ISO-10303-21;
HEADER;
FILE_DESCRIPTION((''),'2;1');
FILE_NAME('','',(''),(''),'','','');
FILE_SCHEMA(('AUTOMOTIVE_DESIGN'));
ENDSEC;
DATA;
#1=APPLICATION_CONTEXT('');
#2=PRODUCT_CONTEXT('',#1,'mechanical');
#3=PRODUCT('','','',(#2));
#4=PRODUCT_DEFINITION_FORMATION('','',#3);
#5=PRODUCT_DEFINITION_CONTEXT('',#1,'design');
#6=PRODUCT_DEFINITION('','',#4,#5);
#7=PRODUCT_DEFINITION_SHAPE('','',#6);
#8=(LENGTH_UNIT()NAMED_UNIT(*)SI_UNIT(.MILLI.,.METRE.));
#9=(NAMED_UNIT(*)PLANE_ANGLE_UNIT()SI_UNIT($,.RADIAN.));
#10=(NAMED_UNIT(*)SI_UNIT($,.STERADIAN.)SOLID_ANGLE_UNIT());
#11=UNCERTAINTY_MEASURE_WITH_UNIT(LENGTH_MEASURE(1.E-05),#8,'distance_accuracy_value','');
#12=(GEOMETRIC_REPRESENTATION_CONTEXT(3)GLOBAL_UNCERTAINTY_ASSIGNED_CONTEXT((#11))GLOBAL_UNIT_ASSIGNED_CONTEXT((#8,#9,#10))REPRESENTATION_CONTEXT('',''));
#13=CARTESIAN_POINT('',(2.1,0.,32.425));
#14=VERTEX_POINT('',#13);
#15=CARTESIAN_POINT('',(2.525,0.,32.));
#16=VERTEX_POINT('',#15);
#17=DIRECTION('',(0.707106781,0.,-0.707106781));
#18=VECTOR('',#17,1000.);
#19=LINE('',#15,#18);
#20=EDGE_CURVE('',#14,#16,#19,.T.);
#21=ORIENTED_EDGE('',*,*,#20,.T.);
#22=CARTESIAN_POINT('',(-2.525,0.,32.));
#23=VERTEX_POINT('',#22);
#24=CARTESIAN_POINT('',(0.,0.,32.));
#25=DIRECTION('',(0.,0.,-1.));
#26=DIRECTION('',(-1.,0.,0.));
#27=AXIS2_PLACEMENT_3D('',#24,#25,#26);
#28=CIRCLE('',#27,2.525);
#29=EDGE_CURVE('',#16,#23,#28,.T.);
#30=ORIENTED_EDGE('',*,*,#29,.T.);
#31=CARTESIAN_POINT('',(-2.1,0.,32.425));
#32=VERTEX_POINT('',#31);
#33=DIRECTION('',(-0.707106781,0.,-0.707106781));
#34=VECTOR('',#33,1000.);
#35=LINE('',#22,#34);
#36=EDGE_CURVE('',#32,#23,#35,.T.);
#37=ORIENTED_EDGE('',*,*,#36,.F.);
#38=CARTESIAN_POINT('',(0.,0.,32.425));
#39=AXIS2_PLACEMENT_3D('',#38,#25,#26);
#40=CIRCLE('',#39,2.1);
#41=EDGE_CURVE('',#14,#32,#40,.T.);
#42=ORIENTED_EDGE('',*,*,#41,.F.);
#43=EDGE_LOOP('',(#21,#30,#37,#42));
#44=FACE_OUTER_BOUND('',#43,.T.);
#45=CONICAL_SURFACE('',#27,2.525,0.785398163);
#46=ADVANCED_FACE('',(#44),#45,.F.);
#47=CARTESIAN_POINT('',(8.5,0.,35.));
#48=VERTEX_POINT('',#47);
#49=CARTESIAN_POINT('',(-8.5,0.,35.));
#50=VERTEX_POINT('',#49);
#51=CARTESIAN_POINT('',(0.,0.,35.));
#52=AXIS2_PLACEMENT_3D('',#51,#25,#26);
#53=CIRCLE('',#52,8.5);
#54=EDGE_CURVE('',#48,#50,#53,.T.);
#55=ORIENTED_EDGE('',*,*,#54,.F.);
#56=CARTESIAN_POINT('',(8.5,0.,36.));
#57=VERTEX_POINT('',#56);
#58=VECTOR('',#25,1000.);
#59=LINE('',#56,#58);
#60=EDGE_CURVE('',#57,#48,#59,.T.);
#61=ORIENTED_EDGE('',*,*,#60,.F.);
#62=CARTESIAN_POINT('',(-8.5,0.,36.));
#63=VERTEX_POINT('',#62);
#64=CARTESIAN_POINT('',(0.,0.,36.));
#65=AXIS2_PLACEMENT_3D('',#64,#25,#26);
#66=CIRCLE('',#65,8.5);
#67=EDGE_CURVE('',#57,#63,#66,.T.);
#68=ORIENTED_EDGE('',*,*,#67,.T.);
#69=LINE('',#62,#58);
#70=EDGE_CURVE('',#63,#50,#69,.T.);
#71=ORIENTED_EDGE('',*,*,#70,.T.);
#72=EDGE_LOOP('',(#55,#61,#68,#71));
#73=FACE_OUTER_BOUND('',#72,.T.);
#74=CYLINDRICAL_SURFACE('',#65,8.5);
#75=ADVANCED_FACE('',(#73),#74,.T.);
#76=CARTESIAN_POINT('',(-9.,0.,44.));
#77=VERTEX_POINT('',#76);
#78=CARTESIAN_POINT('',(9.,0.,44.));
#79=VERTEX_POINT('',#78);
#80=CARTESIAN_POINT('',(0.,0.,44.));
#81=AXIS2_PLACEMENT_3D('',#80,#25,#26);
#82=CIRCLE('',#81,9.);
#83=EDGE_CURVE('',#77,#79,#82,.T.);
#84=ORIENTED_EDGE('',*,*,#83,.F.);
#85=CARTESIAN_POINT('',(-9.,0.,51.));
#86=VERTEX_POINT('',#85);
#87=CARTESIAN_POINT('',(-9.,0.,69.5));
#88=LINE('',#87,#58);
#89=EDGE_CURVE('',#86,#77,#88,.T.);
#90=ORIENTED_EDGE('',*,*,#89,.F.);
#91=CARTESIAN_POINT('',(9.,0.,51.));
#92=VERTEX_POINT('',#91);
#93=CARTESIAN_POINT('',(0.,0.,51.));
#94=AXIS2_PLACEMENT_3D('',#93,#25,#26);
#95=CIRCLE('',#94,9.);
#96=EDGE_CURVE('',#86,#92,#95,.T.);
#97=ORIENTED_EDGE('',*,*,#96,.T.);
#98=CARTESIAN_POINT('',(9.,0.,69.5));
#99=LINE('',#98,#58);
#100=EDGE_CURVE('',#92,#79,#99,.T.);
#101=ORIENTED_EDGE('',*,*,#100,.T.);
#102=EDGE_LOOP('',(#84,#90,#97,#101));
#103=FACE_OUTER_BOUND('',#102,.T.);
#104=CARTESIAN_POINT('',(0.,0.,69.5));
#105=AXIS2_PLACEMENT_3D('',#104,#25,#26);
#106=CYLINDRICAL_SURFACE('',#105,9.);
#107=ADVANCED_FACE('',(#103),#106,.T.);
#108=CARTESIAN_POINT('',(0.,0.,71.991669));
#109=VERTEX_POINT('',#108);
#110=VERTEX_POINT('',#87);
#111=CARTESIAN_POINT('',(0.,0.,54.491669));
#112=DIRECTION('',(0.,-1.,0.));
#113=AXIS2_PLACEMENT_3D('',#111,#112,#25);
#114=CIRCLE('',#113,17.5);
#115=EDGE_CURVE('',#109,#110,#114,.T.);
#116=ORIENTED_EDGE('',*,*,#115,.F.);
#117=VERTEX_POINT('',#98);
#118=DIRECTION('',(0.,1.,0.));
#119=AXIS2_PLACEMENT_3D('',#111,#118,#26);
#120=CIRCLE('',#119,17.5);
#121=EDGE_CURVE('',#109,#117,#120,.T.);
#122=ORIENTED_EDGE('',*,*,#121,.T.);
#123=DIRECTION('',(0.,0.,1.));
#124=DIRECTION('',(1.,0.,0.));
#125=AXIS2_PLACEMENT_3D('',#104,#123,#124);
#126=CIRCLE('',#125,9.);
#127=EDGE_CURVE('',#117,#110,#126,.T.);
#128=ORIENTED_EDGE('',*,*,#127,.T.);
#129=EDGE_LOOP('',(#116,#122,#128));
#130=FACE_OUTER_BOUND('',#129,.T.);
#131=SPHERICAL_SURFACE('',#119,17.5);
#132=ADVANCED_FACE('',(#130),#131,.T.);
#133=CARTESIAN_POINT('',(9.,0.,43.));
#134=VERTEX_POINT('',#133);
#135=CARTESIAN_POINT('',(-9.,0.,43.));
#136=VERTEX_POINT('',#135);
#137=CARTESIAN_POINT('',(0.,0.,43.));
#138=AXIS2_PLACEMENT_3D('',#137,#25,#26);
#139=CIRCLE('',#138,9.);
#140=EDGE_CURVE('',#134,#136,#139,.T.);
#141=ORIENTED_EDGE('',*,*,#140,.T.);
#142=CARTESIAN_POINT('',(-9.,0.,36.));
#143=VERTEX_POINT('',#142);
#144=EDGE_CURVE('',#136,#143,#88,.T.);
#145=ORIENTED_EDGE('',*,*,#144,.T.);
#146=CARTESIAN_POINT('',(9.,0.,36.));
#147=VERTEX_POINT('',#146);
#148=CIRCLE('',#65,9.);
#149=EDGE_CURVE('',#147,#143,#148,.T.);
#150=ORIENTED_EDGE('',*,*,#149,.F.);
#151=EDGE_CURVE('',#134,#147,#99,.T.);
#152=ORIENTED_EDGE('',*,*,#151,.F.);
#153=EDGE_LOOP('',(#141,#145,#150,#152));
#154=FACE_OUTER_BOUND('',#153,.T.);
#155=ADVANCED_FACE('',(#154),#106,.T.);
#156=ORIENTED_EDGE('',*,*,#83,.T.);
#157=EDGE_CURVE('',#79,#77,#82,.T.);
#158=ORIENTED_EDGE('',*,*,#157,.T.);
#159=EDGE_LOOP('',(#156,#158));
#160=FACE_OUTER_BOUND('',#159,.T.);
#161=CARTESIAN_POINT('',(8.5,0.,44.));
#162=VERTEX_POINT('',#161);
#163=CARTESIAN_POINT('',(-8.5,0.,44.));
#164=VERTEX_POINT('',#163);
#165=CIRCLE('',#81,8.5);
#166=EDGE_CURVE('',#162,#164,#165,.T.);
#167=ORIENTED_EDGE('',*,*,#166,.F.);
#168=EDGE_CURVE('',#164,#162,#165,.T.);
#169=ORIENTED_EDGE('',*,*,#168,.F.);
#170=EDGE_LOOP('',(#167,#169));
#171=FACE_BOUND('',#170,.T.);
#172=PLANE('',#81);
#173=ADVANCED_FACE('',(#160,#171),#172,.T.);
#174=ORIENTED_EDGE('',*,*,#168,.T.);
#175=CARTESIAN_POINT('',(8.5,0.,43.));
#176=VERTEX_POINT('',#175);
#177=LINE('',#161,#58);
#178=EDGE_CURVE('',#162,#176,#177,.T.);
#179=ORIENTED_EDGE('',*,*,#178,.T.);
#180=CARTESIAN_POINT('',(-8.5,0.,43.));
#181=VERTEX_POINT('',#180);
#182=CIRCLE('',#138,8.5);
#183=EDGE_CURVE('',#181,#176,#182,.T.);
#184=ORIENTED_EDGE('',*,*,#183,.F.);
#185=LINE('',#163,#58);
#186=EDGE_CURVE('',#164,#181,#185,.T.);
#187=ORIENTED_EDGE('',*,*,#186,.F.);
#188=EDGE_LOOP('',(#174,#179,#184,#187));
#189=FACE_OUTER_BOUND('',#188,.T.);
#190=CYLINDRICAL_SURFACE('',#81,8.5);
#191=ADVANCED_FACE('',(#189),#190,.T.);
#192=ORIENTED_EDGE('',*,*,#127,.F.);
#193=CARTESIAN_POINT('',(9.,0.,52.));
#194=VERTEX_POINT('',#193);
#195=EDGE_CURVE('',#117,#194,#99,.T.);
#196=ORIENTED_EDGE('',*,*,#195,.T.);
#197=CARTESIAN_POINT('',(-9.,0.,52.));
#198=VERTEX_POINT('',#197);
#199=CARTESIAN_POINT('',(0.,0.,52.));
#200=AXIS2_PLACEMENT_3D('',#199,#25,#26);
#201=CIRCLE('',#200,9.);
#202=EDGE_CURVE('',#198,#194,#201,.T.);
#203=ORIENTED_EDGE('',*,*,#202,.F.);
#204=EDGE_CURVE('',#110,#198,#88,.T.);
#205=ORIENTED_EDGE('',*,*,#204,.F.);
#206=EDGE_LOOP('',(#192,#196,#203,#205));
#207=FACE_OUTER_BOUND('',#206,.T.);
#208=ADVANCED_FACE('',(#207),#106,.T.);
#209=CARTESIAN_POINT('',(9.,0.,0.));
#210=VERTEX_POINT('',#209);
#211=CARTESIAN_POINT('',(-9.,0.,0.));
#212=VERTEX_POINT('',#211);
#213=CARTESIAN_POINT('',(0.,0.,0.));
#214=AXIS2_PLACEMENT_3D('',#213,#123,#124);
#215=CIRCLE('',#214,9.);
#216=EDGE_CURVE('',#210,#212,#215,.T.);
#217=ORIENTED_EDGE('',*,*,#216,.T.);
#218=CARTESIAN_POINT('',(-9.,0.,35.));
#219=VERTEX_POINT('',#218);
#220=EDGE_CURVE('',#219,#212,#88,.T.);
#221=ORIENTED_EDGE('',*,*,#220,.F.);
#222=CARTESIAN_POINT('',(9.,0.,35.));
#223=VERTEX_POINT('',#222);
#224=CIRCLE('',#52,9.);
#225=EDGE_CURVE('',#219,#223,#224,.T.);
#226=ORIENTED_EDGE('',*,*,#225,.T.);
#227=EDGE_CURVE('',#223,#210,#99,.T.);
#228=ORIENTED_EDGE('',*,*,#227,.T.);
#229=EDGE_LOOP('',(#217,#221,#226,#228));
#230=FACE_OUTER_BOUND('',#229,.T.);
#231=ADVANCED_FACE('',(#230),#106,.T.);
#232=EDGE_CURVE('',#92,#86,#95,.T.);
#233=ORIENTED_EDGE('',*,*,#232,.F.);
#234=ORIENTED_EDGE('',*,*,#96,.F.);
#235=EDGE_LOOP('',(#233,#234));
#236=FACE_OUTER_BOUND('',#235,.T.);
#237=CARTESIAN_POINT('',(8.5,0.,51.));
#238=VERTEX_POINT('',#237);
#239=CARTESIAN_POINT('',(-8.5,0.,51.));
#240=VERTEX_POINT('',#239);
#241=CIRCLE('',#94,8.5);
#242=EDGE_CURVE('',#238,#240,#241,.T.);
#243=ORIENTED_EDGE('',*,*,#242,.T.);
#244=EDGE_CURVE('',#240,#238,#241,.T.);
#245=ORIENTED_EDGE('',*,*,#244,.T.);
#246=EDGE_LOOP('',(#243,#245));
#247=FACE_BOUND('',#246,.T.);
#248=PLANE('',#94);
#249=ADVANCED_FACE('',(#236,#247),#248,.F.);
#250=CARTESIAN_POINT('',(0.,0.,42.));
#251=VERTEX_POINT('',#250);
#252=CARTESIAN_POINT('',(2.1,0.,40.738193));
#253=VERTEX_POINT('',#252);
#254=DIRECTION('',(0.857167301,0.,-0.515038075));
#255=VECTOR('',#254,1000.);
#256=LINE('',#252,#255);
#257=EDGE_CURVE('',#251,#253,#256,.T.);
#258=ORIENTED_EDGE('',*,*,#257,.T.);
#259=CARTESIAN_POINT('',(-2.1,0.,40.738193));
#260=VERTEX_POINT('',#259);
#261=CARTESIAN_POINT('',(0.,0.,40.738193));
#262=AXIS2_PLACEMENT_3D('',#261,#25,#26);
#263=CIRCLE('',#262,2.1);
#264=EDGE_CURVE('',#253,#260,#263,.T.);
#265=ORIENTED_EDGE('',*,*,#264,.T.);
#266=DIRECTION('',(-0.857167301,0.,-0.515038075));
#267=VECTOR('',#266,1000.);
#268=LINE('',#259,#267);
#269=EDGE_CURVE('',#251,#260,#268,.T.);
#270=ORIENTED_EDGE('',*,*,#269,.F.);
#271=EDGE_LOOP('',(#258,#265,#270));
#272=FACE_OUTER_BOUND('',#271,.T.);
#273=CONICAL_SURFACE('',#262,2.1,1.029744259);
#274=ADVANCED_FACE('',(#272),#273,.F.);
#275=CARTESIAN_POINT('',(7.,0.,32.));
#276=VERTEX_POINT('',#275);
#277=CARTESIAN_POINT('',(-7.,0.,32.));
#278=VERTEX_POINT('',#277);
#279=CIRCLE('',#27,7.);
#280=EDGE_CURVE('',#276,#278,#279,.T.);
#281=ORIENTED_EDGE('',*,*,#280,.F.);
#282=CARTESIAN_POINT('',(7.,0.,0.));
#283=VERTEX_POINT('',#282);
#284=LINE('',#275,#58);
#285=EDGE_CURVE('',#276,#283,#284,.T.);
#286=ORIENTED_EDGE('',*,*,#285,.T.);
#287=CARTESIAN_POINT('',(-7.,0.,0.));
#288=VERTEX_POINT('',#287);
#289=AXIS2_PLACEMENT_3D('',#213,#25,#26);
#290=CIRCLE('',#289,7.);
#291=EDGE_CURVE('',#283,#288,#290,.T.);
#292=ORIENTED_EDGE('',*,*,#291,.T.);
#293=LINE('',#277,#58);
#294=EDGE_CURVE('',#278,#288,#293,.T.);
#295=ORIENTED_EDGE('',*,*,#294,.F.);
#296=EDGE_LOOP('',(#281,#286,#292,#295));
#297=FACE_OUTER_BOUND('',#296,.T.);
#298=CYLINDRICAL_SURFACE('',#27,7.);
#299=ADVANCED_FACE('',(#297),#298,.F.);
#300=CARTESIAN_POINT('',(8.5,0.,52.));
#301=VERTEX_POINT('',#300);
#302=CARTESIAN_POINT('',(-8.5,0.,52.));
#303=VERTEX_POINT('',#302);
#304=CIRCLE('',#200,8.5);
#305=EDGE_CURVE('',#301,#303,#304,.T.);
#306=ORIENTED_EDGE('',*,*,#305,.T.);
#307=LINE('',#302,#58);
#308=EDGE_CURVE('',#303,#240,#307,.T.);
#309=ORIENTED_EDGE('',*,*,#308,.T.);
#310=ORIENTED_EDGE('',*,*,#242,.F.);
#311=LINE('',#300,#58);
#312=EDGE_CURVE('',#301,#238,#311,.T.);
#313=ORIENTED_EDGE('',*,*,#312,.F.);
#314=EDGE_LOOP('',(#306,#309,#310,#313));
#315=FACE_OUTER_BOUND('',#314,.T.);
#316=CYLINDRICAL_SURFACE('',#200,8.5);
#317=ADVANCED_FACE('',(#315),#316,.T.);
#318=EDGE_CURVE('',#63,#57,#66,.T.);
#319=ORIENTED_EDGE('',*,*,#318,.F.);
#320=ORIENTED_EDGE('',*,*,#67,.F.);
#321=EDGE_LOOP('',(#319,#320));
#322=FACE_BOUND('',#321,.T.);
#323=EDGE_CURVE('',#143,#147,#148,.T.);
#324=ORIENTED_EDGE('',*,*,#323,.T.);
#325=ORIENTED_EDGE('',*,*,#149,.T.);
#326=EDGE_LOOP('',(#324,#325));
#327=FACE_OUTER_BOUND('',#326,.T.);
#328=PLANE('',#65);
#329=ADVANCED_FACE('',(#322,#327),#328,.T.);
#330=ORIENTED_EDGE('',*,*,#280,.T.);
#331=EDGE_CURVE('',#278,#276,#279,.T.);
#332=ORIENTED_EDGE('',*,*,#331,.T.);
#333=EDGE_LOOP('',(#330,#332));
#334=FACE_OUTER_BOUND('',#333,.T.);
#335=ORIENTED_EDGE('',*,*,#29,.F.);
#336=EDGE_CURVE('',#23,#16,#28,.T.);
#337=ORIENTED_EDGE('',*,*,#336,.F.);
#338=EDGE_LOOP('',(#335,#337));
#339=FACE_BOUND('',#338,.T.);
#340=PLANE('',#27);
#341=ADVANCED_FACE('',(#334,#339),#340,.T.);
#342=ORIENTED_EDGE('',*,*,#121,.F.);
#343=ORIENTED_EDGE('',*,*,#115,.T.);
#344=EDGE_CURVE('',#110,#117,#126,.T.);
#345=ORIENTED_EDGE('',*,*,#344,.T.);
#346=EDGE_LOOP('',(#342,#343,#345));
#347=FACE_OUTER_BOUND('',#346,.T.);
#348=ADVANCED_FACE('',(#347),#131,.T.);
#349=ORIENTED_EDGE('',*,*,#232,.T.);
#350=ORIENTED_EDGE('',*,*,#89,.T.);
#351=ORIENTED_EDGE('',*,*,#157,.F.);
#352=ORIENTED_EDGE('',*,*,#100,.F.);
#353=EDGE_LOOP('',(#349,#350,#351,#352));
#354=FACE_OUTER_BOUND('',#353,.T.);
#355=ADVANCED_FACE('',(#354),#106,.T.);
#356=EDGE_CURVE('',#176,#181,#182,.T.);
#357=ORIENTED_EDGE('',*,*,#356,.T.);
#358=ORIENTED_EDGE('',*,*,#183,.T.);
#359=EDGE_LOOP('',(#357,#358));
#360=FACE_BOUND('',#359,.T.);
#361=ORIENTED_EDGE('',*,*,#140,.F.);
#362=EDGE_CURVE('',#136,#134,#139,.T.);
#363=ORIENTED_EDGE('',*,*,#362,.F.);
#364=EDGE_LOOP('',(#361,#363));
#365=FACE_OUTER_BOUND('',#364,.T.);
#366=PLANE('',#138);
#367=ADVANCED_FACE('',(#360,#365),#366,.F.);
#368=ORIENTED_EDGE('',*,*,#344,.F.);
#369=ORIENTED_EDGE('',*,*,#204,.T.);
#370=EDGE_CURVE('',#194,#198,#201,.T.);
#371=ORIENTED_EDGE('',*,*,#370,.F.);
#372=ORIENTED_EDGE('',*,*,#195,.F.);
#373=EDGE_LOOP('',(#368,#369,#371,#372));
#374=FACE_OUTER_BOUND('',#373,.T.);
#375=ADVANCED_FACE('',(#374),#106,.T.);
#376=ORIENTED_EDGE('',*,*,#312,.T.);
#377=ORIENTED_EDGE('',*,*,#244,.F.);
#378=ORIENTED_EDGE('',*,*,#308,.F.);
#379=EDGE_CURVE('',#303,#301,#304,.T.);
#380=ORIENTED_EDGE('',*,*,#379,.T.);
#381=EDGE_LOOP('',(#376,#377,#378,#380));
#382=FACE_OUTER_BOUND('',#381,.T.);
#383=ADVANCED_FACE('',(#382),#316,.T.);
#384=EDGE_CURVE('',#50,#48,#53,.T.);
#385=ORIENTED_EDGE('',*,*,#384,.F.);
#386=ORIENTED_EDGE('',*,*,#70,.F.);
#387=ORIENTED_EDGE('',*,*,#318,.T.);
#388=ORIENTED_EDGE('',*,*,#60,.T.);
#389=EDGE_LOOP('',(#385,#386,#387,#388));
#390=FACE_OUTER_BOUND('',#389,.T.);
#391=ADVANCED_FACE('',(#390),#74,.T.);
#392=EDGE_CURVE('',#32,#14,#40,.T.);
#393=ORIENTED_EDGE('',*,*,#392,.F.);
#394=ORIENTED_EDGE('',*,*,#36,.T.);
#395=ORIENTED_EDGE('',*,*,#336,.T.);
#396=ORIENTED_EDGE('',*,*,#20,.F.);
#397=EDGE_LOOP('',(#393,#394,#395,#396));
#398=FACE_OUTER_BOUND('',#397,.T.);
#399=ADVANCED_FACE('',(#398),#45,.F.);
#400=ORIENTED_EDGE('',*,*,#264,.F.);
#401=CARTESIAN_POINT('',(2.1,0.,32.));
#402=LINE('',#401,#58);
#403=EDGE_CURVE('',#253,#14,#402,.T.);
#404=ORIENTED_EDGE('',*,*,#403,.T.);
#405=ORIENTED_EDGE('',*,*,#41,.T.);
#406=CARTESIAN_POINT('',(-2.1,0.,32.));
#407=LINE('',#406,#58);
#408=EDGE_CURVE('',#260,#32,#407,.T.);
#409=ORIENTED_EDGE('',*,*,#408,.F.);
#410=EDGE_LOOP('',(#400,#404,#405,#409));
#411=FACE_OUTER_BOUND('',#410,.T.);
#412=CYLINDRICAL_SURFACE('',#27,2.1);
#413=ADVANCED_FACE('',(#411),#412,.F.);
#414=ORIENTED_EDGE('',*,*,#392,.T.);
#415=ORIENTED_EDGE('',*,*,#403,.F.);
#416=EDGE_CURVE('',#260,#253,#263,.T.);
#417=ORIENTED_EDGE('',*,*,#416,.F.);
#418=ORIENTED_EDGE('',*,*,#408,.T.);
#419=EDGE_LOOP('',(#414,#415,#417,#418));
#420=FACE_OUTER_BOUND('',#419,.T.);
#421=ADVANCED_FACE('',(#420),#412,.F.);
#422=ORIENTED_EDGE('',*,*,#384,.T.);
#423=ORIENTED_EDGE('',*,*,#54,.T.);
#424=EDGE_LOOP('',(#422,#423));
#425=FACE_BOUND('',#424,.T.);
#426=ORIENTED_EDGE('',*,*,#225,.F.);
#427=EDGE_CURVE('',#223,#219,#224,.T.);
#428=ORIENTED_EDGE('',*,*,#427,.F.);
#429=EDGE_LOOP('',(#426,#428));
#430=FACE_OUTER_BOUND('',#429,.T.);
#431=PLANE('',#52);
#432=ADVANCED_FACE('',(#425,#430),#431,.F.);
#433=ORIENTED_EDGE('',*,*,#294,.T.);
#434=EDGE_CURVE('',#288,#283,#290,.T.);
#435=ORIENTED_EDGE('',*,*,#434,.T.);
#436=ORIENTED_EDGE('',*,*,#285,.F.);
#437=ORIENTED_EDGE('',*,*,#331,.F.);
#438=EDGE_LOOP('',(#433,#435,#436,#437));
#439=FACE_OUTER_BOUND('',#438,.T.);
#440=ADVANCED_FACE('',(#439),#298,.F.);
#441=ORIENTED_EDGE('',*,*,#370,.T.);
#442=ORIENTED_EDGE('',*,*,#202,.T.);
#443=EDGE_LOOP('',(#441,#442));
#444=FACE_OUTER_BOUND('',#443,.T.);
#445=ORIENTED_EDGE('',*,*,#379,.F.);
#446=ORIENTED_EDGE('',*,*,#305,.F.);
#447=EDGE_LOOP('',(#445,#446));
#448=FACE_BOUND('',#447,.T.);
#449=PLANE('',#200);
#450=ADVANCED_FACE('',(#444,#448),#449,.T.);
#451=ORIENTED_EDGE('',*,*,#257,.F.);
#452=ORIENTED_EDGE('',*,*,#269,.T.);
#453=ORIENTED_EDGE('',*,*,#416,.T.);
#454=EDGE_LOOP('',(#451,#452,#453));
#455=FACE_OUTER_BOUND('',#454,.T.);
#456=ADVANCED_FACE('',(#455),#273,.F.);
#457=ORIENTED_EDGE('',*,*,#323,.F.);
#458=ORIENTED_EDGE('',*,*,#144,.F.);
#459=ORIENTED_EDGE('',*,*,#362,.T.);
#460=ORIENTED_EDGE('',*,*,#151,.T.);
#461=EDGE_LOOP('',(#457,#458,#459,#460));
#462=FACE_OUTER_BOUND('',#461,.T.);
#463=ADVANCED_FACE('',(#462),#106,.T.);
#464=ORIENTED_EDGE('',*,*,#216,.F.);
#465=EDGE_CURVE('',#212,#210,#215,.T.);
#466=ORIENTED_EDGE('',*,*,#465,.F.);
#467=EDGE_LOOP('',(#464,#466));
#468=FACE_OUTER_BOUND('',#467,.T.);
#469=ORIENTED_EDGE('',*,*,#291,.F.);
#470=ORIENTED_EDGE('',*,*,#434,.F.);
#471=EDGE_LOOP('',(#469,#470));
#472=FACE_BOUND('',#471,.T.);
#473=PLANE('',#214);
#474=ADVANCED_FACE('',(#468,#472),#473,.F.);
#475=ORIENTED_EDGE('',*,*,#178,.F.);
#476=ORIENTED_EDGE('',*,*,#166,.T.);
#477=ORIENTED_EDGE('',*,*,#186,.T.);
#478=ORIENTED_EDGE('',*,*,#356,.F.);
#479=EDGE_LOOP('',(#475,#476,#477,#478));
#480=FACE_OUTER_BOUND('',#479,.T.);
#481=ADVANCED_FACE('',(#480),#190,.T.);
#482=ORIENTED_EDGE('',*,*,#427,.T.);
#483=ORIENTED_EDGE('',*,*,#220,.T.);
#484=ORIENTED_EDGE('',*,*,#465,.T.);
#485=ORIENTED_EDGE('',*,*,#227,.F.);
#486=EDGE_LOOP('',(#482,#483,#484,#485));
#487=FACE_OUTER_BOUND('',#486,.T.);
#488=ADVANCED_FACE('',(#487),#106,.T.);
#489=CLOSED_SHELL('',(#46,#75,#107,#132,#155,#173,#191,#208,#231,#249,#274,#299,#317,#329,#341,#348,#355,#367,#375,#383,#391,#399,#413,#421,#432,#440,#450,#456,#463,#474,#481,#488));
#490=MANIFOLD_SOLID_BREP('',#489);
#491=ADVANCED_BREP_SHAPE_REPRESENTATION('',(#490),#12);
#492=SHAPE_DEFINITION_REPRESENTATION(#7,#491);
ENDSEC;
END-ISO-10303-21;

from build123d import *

# Parameters (mm, degrees)
SKETCH1_R                   = 9
BOSS_EXTRUDE1_DEPTH         = 69.5
SKETCH2_R                   = 7
CUT_EXTRUDE1_DEPTH          = 32
CUT_EXTRUDE3_START          = -35
SKETCH3_R                   = 9
SKETCH3_R_2                 = 8.5
CUT_EXTRUDE3_DEPTH          = 1
CUT_EXTRUDE4_START          = -7
SKETCH4_R                   = 9
SKETCH4_R_2                 = 8.5
CUT_EXTRUDE4_DEPTH          = 1
CUT_EXTRUDE5_START          = -7
SKETCH5_R                   = 9
SKETCH5_R_2                 = 8.5
CUT_EXTRUDE5_DEPTH          = 1
M5_TAPPED_HOLE1_D           = 4.2
M5_TAPPED_HOLE1_DEPTH       = 8.7381927
M5_TAPPED_HOLE1_CSINK_D     = 5.05
M5_TAPPED_HOLE1_CSINK_ANGLE = 90
M5_TAPPED_HOLE1_TIP         = 1.2618073


with BuildPart() as part:
    # Sketch1 → Boss-Extrude1 (new body)
    with BuildSketch(Plane.XY):
        Circle(SKETCH1_R)
    extrude(amount=BOSS_EXTRUDE1_DEPTH)

    # Sketch2 → Cut-Extrude1 (cut)
    with BuildSketch(Plane(origin=(0, 0, 0), x_dir=(-1, 0, 0), z_dir=(0, 0, -1))):
        Circle(SKETCH2_R)
    extrude(amount=-CUT_EXTRUDE1_DEPTH, mode=Mode.SUBTRACT)

    # Sketch3 → Cut-Extrude3 (cut)
    with BuildSketch(Plane(origin=(0, 0, 0), x_dir=(-1, 0, 0), z_dir=(0, 0, -1)).offset(CUT_EXTRUDE3_START)):
        Circle(SKETCH3_R)
        Circle(SKETCH3_R_2, mode=Mode.SUBTRACT)
    extrude(amount=-CUT_EXTRUDE3_DEPTH, mode=Mode.SUBTRACT)

    # Sketch4 → Cut-Extrude4 (cut)
    with BuildSketch(Plane(origin=(0, 0, 36), x_dir=(-1, 0, 0), z_dir=(0, 0, -1)).offset(CUT_EXTRUDE4_START)):
        Circle(SKETCH4_R)
        Circle(SKETCH4_R_2, mode=Mode.SUBTRACT)
    extrude(amount=-CUT_EXTRUDE4_DEPTH, mode=Mode.SUBTRACT)

    # Sketch5 → Cut-Extrude5 (cut)
    with BuildSketch(Plane(origin=(0, 0, 44), x_dir=(-1, 0, 0), z_dir=(0, 0, -1)).offset(CUT_EXTRUDE5_START)):
        Circle(SKETCH5_R)
        Circle(SKETCH5_R_2, mode=Mode.SUBTRACT)
    extrude(amount=-CUT_EXTRUDE5_DEPTH, mode=Mode.SUBTRACT)

    # Sketch6 → Revolve1 (revolve)
    with BuildSketch(Plane(origin=(0, 0, 0), x_dir=(1, 0, 0), z_dir=(0, 1, 0))):
        with BuildLine():
            Line((0, -69.5), (0, -71.99166898))
            ThreePointArc((0, -71.99166898), (-4.669272275, -71.357252173), (-9, -69.5))
            Line((-9, -69.5), (0, -69.5))
        make_face()
    revolve(axis=Axis((0, 0, 0), (0, 0, 1)))

    # M5 Tapped Hole1
    with Locations(Plane(origin=(0, 0, 32), x_dir=(-1, 0, 0), z_dir=(0, 0, -1))):
        with Locations((0, 0)):
            CounterSinkHole(M5_TAPPED_HOLE1_D / 2, M5_TAPPED_HOLE1_CSINK_D / 2, depth=M5_TAPPED_HOLE1_DEPTH, counter_sink_angle=M5_TAPPED_HOLE1_CSINK_ANGLE)
            with Locations((0, 0, -(M5_TAPPED_HOLE1_DEPTH + M5_TAPPED_HOLE1_TIP / 2))):  # 118° drill point
                Cone(0, M5_TAPPED_HOLE1_D / 2, M5_TAPPED_HOLE1_TIP, mode=Mode.SUBTRACT)


solid = part.part
